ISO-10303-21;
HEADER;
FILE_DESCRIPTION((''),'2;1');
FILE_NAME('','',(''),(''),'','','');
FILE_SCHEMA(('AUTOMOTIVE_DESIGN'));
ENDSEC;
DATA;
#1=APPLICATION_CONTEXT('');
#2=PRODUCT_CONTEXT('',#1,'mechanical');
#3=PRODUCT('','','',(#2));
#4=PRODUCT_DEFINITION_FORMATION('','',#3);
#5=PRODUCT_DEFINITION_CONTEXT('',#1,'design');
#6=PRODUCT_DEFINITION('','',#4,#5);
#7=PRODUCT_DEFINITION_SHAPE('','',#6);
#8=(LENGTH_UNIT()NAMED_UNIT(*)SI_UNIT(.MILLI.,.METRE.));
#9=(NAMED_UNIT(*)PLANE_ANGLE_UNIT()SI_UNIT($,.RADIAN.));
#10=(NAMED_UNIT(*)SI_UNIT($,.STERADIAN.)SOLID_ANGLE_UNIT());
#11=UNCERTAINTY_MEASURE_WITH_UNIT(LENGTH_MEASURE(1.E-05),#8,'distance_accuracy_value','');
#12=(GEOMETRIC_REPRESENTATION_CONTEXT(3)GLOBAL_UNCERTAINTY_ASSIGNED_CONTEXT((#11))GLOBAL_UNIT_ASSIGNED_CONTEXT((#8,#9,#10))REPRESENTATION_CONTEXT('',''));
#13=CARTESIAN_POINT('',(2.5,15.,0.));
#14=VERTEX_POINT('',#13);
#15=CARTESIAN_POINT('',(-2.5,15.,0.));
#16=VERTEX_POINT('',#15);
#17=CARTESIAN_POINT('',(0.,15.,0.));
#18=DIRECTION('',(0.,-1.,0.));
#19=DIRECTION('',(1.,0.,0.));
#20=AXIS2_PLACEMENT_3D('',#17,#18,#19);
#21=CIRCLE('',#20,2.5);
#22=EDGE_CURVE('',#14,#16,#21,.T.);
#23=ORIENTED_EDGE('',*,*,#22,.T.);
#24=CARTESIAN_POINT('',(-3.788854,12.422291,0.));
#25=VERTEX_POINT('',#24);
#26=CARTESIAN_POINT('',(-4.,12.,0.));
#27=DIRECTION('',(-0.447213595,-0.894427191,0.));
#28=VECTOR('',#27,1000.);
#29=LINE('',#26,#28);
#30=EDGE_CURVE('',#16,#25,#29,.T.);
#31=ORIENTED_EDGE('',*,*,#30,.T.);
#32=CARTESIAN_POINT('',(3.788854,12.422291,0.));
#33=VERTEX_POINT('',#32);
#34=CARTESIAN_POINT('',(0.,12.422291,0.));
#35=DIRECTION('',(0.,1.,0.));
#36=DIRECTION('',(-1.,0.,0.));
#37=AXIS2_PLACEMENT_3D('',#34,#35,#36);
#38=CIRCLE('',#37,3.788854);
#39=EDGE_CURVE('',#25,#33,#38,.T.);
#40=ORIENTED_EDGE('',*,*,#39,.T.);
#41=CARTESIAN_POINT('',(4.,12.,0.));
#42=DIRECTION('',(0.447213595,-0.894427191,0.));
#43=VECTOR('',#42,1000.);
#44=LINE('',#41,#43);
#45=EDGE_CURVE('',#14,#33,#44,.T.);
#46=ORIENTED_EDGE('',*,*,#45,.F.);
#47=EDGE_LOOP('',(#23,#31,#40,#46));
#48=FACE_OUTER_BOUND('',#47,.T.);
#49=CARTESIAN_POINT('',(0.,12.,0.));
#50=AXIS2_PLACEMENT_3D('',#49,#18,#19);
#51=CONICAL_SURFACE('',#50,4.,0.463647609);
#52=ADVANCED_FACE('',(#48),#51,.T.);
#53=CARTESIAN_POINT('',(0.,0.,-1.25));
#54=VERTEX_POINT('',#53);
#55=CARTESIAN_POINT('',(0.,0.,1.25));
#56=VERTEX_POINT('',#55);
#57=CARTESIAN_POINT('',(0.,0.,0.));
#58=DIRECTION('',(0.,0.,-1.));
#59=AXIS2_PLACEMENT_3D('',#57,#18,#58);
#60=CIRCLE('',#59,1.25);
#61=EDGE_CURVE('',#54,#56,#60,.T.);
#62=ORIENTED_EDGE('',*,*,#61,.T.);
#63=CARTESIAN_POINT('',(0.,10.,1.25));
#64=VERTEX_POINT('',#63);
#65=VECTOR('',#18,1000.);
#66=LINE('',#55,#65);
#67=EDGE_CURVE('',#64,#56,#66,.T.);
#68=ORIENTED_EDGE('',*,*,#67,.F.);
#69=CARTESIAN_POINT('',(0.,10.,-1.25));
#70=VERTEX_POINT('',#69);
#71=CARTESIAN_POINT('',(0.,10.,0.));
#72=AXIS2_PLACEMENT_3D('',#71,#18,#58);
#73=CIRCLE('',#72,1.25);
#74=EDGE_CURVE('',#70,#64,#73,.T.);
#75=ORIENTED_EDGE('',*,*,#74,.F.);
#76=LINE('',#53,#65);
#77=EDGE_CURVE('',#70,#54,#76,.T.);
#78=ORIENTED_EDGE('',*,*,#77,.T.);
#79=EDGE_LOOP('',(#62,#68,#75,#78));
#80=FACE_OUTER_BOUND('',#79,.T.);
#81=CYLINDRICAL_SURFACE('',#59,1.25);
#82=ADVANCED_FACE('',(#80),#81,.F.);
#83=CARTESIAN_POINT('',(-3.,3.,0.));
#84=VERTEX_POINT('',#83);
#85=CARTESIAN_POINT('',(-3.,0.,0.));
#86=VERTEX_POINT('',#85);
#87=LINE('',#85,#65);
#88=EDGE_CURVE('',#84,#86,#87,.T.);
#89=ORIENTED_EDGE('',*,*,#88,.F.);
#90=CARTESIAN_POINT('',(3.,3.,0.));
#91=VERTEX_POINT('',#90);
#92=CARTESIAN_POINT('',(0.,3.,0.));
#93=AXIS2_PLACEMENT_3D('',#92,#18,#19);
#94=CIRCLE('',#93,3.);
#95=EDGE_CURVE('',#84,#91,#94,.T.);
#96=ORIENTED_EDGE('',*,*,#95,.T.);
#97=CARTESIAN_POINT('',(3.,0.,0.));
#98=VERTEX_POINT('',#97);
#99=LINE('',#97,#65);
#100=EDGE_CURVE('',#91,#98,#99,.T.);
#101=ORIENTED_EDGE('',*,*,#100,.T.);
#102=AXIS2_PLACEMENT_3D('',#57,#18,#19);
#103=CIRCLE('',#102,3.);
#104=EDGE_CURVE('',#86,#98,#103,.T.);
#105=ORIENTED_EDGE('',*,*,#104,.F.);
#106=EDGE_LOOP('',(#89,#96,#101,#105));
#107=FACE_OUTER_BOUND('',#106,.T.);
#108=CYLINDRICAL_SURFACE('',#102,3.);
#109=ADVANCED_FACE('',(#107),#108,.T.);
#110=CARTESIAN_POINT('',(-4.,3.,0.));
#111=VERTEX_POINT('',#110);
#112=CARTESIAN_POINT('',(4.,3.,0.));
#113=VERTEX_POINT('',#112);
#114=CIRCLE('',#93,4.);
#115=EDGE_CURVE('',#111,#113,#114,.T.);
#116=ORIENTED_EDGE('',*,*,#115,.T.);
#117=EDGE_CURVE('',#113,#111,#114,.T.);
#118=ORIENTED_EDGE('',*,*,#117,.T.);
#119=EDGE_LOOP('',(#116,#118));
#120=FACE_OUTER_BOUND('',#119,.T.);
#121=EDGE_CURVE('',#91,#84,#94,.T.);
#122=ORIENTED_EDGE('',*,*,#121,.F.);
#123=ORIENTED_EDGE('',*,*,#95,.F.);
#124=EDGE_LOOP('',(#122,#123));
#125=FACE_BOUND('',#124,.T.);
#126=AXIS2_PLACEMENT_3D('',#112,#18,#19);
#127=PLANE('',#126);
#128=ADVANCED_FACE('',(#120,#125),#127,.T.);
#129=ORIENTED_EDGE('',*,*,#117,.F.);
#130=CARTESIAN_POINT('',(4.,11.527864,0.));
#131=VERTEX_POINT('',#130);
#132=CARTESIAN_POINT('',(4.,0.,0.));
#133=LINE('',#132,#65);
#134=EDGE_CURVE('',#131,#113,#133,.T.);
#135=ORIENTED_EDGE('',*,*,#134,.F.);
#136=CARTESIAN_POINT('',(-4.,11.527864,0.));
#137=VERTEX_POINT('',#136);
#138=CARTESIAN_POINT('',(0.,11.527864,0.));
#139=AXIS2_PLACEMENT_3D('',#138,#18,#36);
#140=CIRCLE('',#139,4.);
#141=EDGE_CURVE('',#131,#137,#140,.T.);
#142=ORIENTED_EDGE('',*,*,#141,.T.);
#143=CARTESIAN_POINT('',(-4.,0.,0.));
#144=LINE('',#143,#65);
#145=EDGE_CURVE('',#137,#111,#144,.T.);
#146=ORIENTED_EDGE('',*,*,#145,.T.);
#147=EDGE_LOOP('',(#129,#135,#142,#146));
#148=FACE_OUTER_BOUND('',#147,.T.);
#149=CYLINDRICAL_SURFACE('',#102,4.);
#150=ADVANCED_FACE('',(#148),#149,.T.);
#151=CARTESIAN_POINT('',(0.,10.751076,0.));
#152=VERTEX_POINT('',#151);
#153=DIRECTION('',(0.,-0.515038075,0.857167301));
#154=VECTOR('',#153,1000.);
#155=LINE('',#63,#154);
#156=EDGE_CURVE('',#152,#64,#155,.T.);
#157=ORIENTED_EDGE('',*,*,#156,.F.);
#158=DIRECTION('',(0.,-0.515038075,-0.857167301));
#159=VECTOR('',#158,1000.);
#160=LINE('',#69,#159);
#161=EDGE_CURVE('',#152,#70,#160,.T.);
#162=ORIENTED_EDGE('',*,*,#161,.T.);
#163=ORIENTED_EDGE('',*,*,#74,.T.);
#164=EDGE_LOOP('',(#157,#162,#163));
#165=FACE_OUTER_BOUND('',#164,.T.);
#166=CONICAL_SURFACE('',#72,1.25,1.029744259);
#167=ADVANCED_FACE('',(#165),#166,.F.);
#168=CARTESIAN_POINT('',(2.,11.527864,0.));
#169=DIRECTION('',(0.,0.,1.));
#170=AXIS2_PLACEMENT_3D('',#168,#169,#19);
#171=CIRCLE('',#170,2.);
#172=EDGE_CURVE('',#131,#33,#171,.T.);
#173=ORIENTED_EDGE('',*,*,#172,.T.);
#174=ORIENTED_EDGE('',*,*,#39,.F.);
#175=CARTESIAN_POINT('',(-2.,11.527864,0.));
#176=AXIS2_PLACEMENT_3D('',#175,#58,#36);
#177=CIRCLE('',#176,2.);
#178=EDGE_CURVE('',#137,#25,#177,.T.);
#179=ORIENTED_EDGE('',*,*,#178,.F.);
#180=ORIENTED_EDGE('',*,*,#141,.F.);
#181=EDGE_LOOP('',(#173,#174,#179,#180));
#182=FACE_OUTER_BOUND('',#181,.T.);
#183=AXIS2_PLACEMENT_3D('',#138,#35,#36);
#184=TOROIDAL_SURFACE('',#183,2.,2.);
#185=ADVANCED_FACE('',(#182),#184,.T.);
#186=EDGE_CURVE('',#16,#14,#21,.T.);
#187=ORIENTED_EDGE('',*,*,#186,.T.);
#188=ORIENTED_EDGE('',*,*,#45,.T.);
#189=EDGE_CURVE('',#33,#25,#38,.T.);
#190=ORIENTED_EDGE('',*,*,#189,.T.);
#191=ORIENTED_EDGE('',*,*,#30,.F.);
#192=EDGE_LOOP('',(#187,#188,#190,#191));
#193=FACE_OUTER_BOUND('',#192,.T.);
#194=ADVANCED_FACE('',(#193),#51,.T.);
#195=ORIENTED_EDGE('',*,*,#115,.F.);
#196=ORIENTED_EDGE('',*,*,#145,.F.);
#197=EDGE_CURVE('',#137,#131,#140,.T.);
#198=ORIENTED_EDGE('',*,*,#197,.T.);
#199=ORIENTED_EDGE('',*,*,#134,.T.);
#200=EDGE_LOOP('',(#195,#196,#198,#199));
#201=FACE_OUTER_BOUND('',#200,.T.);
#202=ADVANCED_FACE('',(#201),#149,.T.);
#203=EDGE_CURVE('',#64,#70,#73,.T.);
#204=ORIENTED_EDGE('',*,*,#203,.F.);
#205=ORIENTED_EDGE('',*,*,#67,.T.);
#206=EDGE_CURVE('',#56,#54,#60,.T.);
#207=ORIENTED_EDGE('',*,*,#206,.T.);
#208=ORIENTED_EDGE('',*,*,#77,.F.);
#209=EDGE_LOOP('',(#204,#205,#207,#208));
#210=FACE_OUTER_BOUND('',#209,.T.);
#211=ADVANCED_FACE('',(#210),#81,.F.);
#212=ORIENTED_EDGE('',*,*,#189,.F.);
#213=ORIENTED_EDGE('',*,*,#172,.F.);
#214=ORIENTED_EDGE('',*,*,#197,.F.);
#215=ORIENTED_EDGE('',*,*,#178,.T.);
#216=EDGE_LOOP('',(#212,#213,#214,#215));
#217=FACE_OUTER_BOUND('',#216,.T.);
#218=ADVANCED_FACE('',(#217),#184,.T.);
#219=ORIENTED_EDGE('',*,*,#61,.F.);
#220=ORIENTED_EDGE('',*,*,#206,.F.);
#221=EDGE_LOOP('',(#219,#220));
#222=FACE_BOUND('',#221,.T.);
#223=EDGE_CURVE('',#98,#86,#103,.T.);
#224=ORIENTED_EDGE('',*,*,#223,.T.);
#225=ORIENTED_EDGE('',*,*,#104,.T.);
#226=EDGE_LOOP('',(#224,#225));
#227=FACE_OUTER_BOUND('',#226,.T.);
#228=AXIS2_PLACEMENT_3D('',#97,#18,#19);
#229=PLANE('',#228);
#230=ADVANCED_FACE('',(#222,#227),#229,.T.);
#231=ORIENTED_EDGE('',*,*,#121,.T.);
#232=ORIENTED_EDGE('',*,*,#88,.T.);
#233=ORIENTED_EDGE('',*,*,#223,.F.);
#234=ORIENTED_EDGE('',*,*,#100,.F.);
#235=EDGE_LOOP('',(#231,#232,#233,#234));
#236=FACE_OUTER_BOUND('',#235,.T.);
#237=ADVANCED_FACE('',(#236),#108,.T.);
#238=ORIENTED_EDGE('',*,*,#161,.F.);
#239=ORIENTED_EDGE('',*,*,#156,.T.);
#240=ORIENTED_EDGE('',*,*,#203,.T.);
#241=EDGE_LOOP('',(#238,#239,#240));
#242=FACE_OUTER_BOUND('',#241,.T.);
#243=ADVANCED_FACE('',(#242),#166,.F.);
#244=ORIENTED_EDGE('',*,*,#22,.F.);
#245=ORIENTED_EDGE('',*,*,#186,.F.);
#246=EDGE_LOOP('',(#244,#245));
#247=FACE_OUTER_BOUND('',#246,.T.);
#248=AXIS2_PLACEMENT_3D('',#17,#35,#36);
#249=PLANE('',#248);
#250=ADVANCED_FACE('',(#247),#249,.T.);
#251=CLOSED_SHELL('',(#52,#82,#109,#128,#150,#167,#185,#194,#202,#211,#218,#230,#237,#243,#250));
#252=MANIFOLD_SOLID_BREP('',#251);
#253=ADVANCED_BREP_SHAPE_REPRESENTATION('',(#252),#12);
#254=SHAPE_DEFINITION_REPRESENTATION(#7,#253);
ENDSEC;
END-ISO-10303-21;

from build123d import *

# Parameters (mm, degrees)
M3_TAPPED_HOLE1_D     = 2.5
M3_TAPPED_HOLE1_DEPTH = 10
M3_TAPPED_HOLE1_TIP   = 0.751075774
FILLET1_R             = 2


with BuildPart() as part:
    # Sketch1 → Revolve1 (revolve)
    with BuildSketch(Plane.XY):
        Polygon((0, 0), (0, 15), (2.5, 15), (4, 12), (4, 3), (3, 3), (3, 0), align=None)
    revolve(axis=Axis((0, 0, 0), (0, 1, 0)))

    # M3 Tapped Hole1
    with Locations(Plane(origin=(0, 0, 0), x_dir=(-1, 0, 0), z_dir=(0, -1, 0))):
        with Locations((0, 0)):
            Hole(M3_TAPPED_HOLE1_D / 2, depth=M3_TAPPED_HOLE1_DEPTH)
            with Locations((0, 0, -(M3_TAPPED_HOLE1_DEPTH + M3_TAPPED_HOLE1_TIP / 2))):  # 118° drill point
                Cone(0, M3_TAPPED_HOLE1_D / 2, M3_TAPPED_HOLE1_TIP, mode=Mode.SUBTRACT)

    # Fillet1
    fillet1_edges = [part.edges().sort_by_distance(p)[0] for p in [
        (-4, 12, 0),
    ]]
    fillet(fillet1_edges, radius=FILLET1_R)


solid = part.part
